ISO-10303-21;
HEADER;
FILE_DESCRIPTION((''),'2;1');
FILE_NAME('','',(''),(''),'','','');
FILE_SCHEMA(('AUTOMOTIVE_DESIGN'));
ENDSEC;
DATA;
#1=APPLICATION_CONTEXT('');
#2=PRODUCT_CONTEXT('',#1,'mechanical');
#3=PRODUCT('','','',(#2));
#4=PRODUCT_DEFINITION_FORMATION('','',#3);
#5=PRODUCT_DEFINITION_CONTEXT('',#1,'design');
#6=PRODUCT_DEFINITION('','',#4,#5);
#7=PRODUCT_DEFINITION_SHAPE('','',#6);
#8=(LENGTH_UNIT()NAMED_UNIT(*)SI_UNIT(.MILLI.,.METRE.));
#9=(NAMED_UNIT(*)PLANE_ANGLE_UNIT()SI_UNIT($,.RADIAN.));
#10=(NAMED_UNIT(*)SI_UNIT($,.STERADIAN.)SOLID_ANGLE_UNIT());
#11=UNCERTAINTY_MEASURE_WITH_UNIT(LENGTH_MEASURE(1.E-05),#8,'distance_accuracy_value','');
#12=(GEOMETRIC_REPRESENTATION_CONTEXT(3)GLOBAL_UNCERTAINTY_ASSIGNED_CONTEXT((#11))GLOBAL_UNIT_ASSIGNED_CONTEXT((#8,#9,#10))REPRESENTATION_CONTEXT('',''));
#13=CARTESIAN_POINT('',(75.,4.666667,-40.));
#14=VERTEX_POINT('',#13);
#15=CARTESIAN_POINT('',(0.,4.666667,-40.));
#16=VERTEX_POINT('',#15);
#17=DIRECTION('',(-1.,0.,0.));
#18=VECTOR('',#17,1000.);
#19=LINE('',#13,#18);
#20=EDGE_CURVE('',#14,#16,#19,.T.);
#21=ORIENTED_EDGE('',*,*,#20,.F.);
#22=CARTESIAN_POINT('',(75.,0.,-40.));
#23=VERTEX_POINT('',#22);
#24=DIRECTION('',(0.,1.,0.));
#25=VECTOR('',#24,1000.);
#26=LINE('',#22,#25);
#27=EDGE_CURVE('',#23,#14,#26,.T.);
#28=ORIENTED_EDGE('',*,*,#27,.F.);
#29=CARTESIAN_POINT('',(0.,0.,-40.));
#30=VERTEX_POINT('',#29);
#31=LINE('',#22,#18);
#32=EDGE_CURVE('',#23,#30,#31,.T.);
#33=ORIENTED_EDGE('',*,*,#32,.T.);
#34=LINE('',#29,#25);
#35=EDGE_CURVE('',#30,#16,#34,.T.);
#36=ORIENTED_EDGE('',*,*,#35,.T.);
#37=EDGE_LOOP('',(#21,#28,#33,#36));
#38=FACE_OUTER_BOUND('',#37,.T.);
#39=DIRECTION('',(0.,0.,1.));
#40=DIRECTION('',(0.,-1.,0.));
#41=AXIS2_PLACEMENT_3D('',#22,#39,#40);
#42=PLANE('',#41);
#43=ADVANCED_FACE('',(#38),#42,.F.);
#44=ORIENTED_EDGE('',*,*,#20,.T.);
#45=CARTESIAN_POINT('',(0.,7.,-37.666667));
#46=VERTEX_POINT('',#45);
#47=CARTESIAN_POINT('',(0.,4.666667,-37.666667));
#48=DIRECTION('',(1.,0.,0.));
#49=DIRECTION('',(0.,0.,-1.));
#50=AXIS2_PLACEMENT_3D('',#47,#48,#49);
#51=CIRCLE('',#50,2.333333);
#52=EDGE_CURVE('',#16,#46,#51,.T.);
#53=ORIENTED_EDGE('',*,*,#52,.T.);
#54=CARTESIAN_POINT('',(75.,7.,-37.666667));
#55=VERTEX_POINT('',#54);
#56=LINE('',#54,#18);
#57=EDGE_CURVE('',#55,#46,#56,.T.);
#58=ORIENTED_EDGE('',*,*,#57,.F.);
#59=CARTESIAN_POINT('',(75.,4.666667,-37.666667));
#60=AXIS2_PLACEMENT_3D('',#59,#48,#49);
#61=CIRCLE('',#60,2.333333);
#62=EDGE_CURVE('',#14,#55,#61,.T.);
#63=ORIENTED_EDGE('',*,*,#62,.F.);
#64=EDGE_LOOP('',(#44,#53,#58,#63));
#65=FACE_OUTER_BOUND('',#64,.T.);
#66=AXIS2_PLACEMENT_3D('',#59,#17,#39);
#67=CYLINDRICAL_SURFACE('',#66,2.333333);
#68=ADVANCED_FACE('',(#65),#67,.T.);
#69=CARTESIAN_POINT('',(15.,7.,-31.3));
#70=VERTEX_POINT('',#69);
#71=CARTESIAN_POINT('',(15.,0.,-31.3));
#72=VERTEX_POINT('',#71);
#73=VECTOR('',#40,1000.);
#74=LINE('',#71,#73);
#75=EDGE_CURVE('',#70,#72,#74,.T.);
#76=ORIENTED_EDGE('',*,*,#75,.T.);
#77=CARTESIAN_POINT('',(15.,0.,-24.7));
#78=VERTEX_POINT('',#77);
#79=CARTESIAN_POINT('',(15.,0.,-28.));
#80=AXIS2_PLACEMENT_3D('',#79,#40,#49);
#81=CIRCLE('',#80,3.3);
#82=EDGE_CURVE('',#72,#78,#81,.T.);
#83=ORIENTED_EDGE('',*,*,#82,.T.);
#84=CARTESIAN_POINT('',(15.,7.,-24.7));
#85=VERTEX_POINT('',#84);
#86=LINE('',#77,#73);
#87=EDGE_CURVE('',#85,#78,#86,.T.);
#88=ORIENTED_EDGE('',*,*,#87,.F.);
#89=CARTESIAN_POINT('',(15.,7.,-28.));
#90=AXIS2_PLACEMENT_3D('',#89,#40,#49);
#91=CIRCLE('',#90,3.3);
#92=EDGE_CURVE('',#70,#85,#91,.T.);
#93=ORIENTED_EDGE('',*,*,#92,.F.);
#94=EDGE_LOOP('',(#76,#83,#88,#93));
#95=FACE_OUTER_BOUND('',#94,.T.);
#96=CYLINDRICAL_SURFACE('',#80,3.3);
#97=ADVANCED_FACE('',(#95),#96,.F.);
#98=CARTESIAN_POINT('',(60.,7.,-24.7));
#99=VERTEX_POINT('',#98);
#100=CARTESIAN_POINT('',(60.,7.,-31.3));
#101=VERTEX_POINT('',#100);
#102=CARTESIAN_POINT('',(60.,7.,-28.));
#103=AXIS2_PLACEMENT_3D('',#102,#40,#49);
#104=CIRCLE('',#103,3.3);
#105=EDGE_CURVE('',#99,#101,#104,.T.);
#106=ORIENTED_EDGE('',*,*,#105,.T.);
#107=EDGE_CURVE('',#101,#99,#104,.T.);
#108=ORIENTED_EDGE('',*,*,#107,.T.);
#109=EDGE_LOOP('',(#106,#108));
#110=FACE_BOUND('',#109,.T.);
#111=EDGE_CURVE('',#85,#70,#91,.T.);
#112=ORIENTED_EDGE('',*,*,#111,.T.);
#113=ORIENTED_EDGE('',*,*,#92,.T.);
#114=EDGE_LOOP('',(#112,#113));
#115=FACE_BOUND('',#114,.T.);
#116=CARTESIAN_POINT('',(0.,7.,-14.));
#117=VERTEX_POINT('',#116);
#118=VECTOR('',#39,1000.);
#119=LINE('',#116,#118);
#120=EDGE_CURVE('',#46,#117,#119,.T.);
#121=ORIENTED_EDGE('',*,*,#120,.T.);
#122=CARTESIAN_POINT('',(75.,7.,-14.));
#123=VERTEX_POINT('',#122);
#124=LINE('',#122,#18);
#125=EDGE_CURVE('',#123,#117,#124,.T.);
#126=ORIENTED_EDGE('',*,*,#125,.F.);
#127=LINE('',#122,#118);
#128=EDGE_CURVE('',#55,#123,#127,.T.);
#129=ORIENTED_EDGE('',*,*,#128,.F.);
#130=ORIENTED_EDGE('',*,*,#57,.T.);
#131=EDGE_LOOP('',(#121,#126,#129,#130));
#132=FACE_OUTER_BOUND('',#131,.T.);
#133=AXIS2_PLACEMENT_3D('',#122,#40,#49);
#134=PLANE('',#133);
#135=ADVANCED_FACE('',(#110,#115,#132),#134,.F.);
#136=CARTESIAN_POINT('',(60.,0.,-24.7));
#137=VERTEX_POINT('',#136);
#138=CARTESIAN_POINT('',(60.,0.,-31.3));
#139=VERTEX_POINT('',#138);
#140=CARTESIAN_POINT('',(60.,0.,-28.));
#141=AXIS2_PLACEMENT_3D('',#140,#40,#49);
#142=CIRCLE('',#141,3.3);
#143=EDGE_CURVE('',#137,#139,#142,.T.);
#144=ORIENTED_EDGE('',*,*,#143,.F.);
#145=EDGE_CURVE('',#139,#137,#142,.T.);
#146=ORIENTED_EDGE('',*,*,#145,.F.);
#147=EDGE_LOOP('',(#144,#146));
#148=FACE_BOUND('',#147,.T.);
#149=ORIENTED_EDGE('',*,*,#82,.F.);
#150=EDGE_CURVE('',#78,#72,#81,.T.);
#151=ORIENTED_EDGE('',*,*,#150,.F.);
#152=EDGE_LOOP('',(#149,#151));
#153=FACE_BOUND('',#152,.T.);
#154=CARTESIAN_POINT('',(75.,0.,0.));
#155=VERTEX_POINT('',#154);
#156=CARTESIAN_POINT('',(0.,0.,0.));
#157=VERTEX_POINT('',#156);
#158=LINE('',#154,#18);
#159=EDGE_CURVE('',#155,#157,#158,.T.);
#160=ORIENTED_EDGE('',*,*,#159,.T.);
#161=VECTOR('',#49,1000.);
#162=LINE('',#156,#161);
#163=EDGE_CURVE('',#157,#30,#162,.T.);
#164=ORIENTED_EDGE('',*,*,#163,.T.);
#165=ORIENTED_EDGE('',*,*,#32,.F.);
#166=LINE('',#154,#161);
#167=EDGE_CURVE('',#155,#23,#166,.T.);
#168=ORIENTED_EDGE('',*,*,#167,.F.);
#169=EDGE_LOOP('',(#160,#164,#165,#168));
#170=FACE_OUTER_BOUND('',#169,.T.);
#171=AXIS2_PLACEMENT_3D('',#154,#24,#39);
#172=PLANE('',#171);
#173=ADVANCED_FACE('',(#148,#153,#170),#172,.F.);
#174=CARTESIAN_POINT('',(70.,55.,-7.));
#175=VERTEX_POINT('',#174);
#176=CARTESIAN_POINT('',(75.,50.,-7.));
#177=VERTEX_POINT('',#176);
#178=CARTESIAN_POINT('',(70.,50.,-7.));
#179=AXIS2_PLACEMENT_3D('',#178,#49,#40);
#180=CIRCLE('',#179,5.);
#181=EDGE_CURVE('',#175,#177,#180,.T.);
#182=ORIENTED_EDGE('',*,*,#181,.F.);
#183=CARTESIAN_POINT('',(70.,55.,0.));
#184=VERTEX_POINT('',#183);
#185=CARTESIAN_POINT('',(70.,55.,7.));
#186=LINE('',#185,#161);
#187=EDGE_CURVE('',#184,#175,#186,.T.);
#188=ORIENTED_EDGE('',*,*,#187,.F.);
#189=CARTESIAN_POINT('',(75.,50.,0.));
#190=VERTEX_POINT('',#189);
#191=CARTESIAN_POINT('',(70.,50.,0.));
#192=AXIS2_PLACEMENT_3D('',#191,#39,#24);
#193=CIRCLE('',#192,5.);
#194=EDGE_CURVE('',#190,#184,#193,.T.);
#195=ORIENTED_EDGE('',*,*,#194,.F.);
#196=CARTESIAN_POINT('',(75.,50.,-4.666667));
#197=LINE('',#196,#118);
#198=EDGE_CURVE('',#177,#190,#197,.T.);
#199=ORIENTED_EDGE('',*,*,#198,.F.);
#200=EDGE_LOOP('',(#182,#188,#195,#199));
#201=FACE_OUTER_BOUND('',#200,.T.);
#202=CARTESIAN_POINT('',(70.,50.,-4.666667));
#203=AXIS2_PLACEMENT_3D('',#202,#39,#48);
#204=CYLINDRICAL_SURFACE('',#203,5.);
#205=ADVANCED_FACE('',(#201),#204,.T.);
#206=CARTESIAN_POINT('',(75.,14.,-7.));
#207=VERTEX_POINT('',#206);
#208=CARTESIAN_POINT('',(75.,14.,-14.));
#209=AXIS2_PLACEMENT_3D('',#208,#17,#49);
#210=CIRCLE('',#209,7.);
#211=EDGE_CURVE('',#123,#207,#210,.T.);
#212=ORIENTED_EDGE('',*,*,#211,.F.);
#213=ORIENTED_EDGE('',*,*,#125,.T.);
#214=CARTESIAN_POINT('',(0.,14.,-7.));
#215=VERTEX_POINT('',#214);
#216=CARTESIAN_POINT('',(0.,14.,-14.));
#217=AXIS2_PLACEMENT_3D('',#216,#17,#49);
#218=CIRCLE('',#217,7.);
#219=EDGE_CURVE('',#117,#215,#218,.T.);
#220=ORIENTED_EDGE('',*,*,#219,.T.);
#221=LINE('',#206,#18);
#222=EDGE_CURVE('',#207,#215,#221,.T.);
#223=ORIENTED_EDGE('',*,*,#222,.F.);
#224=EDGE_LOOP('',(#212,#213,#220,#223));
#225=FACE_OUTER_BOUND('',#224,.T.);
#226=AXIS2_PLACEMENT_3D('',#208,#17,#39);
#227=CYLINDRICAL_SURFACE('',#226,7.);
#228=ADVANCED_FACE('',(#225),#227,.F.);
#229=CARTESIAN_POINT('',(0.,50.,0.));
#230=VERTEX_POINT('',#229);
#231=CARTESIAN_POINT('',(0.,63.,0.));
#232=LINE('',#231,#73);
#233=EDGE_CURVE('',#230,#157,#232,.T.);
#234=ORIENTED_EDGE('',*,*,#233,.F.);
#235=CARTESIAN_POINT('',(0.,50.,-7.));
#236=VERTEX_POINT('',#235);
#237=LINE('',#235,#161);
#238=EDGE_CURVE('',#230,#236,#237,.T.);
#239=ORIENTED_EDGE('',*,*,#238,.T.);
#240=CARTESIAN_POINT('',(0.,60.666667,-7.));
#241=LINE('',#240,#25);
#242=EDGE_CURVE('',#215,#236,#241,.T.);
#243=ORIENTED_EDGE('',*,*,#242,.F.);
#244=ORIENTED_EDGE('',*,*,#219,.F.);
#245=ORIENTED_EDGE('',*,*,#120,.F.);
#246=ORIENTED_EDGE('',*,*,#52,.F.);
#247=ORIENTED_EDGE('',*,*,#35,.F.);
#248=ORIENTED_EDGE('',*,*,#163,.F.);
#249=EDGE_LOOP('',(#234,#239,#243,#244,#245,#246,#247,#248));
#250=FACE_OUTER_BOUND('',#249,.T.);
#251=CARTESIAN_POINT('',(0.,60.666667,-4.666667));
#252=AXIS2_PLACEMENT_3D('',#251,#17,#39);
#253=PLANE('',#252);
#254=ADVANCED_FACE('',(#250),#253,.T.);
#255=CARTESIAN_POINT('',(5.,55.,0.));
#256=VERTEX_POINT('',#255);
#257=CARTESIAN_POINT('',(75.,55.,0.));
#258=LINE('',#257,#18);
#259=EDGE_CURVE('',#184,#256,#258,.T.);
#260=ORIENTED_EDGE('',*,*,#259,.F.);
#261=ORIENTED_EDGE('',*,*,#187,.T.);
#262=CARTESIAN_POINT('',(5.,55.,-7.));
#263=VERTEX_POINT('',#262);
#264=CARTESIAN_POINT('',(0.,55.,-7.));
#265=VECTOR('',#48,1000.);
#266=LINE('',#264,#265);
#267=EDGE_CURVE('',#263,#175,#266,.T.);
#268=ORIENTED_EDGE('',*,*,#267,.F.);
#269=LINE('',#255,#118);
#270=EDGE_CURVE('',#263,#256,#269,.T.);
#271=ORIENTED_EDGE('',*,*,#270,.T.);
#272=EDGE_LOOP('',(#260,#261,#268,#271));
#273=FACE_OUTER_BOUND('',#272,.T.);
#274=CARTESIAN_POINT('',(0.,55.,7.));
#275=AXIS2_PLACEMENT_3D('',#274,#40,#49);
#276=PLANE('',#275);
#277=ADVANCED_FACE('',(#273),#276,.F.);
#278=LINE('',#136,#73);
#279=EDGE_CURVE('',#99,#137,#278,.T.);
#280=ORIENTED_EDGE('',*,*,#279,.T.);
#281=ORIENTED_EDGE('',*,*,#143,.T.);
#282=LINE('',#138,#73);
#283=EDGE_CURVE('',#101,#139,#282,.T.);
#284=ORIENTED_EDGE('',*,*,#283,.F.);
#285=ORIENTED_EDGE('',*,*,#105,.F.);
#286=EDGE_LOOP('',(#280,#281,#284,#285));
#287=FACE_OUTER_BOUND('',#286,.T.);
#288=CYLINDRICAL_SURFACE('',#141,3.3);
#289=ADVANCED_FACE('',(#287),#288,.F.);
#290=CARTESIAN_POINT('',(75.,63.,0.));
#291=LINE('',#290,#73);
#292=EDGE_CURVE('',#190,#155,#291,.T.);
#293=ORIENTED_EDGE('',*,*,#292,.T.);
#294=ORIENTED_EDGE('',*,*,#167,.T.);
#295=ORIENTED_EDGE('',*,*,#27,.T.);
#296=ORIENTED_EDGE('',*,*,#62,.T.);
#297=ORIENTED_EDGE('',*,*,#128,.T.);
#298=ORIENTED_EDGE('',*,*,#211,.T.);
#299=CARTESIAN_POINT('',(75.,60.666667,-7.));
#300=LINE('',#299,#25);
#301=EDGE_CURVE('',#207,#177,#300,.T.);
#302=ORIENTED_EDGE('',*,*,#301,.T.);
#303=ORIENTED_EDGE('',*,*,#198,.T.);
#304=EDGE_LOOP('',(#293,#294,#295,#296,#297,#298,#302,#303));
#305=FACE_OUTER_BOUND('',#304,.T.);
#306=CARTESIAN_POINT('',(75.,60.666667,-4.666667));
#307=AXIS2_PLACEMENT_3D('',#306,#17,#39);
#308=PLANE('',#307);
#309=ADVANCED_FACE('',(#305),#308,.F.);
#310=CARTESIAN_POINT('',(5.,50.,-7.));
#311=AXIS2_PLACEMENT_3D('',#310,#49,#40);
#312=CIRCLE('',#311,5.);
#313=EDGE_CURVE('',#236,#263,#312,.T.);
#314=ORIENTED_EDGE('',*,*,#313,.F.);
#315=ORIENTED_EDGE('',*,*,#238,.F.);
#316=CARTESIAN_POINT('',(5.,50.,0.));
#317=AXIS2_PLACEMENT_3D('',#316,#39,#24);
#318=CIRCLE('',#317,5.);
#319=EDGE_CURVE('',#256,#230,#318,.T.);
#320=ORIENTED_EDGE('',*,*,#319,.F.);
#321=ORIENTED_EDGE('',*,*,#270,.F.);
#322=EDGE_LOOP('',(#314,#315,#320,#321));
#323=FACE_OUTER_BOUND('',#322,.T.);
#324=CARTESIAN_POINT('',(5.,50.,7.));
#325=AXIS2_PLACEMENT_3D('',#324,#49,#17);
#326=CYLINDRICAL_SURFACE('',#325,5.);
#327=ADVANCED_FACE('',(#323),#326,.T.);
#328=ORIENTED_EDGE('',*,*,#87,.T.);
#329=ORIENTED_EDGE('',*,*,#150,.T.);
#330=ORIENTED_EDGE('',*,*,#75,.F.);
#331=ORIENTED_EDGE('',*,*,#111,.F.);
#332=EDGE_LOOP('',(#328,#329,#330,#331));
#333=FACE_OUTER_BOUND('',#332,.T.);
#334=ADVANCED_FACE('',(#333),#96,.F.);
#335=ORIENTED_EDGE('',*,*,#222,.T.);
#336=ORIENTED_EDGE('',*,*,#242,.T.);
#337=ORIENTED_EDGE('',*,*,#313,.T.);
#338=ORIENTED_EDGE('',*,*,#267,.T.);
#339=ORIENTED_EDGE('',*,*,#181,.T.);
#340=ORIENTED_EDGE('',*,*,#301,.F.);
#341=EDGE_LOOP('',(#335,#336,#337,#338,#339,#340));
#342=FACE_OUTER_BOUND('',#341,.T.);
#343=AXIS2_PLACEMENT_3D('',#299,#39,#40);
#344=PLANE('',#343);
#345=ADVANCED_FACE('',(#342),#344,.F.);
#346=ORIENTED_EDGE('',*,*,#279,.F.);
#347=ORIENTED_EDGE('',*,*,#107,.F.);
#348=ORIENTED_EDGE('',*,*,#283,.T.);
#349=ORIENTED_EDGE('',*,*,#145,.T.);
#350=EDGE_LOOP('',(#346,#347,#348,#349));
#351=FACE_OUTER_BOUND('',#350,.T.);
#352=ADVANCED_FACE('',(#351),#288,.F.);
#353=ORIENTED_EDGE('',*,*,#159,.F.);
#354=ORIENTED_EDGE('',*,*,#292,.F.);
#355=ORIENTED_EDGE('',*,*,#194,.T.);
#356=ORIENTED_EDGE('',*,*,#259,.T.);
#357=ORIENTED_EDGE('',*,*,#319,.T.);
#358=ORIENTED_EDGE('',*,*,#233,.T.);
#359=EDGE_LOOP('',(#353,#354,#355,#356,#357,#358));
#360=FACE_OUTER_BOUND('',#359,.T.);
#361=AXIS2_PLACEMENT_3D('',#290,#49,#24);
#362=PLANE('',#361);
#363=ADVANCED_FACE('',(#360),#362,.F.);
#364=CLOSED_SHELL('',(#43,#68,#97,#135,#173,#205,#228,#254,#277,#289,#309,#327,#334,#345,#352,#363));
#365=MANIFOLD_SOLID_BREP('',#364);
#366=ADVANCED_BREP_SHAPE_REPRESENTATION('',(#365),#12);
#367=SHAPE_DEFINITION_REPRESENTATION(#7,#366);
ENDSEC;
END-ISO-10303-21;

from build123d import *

# Parameters (mm, degrees)
UNEQUAL_ANGLE_STEEL_6_3_4_1_DEPTH = 75
M6_CLEARANCE_HOLE1_D              = 6.6
M6_CLEARANCE_HOLE1_DEPTH          = 20
M6_CLEARANCE_HOLE1_TIP            = 1.982840043
CUT_EXTRUDE1_DEPTH                = 106.80170131
CUT_EXTRUDE1_DEPTH_BACK           = 106.80170131
SKETCH8_W                         = 14
SKETCH8_H                         = 16
FILLET1_R                         = 5


with BuildPart() as part:
    # Sketch11 → Unequal Angle Steel 6.3-4(1) (new body)
    with BuildSketch(Plane.YZ):
        with BuildLine():
            Line((63, 0), (0, 0))
            Line((0, 0), (0, -40))
            Line((0, -40), (4.666666667, -40))
            ThreePointArc((4.666666667, -40), (6.316582489, -39.316582489), (7, -37.666666667))
            Line((7, -37.666666667), (7, -14))
            ThreePointArc((7, -14), (9.050252532, -9.050252532), (14, -7))
            Line((14, -7), (60.666666667, -7))
            ThreePointArc((60.666666667, -7), (62.316582489, -6.316582489), (63, -4.666666667))
            Line((63, -4.666666667), (63, 0))
        make_face()
    extrude(amount=UNEQUAL_ANGLE_STEEL_6_3_4_1_DEPTH)

    # M6 Clearance Hole1
    with Locations(Plane.XZ):
        with Locations((15, -28), (60, -28)):
            Hole(M6_CLEARANCE_HOLE1_D / 2, depth=M6_CLEARANCE_HOLE1_DEPTH)
            with Locations((0, 0, -(M6_CLEARANCE_HOLE1_DEPTH + M6_CLEARANCE_HOLE1_TIP / 2))):  # 118° drill point
                Cone(0, M6_CLEARANCE_HOLE1_D / 2, M6_CLEARANCE_HOLE1_TIP, mode=Mode.SUBTRACT)

    # Sketch8 → Cut-Extrude1 (cut, two sides: drawn at the far end of the back side and taken through both)
    with BuildSketch(Plane(origin=(75, 0, 0), x_dir=(0, 0, -1), z_dir=(1, 0, 0)).offset(-CUT_EXTRUDE1_DEPTH_BACK)):
        with Locations((0, 63)):
            Rectangle(SKETCH8_W, SKETCH8_H)
    extrude(amount=CUT_EXTRUDE1_DEPTH + CUT_EXTRUDE1_DEPTH_BACK, mode=Mode.SUBTRACT)

    # Fillet1
    fillet1_edges = [part.edges().sort_by_distance(p)[0] for p in [
        (0, 55, -3.5),
        (75, 55, -3.5),
    ]]
    fillet(fillet1_edges, radius=FILLET1_R)


solid = part.part
